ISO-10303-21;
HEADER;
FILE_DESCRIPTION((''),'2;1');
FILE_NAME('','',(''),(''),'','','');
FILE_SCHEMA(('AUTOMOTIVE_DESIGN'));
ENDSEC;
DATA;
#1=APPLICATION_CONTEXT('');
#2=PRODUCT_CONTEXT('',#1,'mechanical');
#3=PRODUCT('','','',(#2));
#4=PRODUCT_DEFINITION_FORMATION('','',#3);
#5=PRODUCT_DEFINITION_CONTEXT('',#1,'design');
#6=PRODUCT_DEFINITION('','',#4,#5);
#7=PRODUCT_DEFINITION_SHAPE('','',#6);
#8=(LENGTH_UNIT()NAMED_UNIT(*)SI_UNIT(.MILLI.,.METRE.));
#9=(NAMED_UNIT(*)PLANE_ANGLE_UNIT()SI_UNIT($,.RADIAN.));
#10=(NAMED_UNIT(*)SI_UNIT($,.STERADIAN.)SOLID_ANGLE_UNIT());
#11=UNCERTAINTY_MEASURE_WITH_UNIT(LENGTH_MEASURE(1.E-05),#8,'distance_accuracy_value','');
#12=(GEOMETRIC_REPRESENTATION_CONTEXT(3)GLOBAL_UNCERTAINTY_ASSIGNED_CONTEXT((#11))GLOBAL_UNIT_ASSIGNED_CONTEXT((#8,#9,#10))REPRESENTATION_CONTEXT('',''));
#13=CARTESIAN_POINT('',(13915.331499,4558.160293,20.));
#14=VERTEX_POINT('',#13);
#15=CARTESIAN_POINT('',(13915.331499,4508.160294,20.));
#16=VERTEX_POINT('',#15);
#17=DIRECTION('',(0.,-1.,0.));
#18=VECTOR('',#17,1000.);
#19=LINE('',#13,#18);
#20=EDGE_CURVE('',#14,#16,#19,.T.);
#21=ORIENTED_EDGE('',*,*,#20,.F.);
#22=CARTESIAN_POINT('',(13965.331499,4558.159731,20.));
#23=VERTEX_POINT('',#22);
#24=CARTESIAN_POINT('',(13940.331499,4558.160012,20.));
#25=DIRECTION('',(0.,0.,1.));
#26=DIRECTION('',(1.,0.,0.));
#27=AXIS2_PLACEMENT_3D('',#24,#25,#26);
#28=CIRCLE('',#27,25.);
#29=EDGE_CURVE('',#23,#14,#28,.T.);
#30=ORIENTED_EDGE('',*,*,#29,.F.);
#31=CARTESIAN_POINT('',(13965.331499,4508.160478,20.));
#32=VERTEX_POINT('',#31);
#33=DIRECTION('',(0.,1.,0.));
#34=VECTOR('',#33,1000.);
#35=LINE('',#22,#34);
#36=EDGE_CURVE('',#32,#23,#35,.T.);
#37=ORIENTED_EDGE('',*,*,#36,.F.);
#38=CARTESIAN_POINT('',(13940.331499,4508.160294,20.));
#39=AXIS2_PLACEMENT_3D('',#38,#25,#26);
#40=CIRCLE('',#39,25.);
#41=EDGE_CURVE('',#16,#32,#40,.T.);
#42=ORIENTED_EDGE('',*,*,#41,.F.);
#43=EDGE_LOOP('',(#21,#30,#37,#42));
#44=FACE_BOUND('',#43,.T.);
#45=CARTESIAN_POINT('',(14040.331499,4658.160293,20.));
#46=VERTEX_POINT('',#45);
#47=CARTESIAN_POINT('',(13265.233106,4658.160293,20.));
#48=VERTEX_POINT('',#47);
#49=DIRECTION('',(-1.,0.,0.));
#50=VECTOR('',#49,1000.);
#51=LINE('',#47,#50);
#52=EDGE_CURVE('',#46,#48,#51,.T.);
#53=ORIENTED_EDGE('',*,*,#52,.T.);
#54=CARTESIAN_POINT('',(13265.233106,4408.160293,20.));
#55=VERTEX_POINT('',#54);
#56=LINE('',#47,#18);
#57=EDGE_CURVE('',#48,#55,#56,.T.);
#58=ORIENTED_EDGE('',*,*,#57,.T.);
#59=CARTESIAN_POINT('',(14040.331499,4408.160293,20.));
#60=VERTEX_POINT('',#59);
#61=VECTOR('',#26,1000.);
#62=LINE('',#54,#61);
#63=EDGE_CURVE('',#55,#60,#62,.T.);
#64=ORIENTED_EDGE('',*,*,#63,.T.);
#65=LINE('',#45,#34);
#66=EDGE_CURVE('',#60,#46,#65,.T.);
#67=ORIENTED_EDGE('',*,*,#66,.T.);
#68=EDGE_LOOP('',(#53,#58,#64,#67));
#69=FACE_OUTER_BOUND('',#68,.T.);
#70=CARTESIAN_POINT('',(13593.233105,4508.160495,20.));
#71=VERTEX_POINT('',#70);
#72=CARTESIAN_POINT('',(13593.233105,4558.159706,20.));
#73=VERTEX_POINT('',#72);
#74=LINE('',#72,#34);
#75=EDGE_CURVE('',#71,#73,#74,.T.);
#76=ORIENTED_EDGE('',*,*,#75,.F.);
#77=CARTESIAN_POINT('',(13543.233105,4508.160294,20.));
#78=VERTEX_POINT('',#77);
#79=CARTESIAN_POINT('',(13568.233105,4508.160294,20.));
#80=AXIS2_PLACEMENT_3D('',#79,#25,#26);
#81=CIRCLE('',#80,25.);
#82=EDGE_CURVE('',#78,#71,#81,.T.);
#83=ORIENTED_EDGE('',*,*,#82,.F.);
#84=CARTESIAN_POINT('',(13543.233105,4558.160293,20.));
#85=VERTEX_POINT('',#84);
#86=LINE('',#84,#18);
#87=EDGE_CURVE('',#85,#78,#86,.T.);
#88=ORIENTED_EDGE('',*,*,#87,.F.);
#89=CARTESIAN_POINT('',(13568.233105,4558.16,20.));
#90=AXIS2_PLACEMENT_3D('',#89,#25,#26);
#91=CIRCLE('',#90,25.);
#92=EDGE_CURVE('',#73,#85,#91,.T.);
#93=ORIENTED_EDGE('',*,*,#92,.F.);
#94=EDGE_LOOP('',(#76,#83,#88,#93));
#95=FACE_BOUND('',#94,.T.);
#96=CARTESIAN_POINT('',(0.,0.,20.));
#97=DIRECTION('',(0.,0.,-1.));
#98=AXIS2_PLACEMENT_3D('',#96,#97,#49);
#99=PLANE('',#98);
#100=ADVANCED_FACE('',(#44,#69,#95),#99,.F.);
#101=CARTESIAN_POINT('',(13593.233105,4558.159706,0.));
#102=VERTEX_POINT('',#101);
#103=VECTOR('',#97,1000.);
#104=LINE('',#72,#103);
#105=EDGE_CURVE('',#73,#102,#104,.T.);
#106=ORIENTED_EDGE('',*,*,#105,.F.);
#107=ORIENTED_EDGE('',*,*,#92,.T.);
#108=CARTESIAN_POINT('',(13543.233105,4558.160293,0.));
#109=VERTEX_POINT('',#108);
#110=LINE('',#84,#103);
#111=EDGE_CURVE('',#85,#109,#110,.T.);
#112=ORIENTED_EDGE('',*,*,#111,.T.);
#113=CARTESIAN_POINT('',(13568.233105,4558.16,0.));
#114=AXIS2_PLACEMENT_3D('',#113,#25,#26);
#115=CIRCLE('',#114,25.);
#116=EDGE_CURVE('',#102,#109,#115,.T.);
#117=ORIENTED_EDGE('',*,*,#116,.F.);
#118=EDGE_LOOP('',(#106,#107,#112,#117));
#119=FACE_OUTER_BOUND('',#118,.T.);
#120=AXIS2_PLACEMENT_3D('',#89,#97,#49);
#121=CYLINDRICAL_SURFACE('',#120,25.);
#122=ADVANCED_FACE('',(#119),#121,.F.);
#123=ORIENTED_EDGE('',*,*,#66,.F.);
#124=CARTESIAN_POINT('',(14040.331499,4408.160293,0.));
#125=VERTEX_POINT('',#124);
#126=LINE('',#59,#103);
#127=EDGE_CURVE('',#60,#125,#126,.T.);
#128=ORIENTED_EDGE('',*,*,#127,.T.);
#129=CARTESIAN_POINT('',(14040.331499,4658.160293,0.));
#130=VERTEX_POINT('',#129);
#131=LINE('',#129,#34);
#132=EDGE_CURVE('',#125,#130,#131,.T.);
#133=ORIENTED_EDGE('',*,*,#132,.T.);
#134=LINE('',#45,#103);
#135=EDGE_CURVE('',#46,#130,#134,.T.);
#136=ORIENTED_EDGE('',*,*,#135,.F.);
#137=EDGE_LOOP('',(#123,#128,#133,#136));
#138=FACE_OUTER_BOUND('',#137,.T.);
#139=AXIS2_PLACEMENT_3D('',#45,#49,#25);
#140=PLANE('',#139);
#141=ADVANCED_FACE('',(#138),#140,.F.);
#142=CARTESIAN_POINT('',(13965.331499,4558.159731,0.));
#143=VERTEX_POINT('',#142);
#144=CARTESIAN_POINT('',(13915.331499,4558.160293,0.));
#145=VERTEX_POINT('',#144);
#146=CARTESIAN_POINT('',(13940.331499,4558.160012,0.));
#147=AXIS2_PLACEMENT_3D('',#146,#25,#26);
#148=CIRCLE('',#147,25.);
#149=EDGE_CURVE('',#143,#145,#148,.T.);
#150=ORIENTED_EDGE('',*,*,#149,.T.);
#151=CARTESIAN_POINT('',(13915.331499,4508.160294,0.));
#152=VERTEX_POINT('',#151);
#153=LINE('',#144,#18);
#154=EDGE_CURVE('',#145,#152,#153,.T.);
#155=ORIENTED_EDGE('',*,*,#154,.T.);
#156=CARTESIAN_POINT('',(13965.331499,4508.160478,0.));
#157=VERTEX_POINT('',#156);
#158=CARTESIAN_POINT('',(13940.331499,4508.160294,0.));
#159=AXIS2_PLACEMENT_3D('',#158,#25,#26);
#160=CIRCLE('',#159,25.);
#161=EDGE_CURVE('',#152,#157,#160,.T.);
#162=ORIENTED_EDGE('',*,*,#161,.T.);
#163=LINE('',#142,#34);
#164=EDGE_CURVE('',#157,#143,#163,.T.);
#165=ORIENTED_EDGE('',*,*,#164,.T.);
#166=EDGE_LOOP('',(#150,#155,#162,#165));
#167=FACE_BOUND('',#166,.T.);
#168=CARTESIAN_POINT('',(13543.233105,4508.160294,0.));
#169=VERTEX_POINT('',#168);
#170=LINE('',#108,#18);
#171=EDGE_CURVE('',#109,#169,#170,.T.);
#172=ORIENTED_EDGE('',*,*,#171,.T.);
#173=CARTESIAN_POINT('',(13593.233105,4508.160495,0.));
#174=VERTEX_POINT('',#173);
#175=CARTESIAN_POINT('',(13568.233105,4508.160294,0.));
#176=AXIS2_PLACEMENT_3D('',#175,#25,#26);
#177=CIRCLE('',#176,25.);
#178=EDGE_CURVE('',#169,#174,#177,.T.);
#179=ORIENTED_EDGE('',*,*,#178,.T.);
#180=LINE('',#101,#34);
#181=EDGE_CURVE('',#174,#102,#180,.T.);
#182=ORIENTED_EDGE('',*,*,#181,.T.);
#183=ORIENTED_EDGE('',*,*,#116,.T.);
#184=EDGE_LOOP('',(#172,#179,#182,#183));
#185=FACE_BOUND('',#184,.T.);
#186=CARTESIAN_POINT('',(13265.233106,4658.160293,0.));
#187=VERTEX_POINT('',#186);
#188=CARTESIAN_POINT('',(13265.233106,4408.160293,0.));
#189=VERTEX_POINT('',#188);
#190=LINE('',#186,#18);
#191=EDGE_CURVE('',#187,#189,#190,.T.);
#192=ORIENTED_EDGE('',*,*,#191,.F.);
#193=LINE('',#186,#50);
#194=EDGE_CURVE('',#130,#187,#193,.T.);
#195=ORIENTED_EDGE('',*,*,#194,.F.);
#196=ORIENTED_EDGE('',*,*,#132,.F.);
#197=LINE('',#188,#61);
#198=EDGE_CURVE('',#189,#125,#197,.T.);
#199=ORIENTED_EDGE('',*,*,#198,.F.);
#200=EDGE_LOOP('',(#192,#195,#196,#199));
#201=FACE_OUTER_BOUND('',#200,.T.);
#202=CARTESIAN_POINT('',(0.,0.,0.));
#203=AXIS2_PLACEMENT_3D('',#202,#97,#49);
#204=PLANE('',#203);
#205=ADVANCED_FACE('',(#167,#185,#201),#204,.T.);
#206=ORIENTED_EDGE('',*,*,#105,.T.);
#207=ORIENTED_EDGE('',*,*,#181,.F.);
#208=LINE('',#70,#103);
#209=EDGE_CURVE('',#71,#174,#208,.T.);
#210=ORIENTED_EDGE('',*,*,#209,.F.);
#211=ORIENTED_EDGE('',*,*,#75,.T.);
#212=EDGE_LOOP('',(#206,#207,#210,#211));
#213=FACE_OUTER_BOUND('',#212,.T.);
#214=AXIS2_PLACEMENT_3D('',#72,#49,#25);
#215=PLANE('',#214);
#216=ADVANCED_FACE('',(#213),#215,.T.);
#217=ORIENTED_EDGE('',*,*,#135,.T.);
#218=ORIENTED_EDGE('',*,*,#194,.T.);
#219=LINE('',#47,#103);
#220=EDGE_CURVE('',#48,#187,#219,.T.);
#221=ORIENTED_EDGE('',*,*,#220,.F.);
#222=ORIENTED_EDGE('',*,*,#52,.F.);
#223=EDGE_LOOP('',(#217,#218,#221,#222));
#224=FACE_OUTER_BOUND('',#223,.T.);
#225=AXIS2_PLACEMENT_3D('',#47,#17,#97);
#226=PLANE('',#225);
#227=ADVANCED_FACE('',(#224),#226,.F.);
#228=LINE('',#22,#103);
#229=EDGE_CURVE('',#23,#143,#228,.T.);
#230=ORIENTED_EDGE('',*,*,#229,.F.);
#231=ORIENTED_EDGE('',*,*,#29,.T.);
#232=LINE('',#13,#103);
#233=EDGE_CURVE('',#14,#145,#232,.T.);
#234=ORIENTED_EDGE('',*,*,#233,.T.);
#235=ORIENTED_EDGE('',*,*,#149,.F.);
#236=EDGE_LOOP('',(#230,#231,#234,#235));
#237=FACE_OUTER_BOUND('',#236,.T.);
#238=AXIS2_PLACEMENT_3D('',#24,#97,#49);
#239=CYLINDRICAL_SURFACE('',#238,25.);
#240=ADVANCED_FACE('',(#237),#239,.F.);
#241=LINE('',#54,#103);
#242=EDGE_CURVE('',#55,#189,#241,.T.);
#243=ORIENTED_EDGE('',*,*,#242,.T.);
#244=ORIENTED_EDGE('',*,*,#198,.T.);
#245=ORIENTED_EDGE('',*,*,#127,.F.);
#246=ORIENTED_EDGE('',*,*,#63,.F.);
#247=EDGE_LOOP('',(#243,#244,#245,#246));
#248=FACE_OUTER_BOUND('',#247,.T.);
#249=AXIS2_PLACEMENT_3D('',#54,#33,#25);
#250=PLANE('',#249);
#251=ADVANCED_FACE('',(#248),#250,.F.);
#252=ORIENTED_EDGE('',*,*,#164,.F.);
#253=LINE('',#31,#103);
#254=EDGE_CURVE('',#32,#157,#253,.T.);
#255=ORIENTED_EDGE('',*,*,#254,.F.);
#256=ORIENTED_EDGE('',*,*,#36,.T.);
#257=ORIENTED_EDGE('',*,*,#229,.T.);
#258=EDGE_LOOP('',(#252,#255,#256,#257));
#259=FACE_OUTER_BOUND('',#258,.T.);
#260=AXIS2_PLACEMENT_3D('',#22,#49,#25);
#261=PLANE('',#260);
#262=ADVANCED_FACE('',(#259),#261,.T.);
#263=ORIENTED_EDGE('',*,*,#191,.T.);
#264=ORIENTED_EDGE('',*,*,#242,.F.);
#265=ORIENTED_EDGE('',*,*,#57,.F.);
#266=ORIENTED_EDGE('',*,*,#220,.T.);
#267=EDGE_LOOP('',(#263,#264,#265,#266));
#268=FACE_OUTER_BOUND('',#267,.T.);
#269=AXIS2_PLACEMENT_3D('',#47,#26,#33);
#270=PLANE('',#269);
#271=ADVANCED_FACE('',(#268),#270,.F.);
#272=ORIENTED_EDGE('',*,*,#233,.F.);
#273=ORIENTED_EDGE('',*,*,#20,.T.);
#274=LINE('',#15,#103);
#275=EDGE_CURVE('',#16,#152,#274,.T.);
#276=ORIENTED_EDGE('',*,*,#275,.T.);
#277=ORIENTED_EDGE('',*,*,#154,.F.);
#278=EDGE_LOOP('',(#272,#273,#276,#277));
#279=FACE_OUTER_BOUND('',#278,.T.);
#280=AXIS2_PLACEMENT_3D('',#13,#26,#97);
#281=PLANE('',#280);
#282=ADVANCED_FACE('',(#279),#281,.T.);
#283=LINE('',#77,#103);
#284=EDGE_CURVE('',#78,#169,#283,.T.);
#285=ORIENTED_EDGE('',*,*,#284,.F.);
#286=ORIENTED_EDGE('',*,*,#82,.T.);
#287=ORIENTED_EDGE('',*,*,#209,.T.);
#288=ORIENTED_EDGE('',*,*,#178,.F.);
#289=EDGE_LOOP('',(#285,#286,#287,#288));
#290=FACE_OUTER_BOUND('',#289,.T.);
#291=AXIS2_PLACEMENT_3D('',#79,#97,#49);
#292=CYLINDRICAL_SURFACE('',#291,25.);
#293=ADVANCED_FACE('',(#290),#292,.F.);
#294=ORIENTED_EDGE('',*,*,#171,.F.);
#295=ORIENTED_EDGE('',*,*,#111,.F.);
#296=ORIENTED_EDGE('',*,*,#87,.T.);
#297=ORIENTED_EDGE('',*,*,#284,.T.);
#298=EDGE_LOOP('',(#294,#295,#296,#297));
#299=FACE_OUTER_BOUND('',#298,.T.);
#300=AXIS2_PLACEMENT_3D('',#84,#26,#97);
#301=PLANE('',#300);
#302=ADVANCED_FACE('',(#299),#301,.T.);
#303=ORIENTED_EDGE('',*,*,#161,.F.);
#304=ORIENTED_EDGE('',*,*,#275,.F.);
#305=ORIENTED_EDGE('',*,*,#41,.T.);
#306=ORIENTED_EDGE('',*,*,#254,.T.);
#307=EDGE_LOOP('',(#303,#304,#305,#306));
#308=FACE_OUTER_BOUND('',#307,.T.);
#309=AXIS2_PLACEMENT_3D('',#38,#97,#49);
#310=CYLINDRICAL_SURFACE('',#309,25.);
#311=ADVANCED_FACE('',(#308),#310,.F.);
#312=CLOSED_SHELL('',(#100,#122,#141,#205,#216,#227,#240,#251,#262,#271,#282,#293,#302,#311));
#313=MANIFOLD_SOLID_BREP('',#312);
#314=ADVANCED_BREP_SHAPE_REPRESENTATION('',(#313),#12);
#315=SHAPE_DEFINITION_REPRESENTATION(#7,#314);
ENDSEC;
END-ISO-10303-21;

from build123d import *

# Parameters (mm, degrees)
BOSS_EXTRUDE1_DEPTH = 20


with BuildPart() as part:
    # Sketch1 → Boss-Extrude1 (new body)
    with BuildSketch(Plane.XY):
        Polygon((14040.331499194, 4658.160293083), (14040.331499194, 4408.160293083), (13265.233105958, 4408.160293083), (13265.233105872, 4658.160293083), align=None)
        with BuildLine():
            Line((13543.233105077, 4558.160293388), (13543.233105077, 4508.160293551))
            ThreePointArc((13543.233105077, 4508.160293551), (13568.233205921, 4483.160293631), (13593.233104917, 4508.160495399))
            Line((13593.233104917, 4508.160495399), (13593.233104917, 4558.159705819))
            ThreePointArc((13593.233104917, 4558.159705819), (13568.233398781, 4583.159999523), (13543.233105077, 4558.160293388))
        make_face(mode=Mode.SUBTRACT)
        with BuildLine():
            Line((13915.331499495, 4558.160293394), (13915.331499495, 4508.160293549))
            ThreePointArc((13915.331499495, 4508.160293549), (13940.331591876, 4483.160293859), (13965.331499344, 4508.160478461))
            Line((13965.331499344, 4508.160478461), (13965.331499344, 4558.159730803))
            ThreePointArc((13965.331499344, 4558.159730803), (13940.331780715, 4583.160012023), (13915.331499495, 4558.160293394))
        make_face(mode=Mode.SUBTRACT)
    extrude(amount=BOSS_EXTRUDE1_DEPTH)


solid = part.part
